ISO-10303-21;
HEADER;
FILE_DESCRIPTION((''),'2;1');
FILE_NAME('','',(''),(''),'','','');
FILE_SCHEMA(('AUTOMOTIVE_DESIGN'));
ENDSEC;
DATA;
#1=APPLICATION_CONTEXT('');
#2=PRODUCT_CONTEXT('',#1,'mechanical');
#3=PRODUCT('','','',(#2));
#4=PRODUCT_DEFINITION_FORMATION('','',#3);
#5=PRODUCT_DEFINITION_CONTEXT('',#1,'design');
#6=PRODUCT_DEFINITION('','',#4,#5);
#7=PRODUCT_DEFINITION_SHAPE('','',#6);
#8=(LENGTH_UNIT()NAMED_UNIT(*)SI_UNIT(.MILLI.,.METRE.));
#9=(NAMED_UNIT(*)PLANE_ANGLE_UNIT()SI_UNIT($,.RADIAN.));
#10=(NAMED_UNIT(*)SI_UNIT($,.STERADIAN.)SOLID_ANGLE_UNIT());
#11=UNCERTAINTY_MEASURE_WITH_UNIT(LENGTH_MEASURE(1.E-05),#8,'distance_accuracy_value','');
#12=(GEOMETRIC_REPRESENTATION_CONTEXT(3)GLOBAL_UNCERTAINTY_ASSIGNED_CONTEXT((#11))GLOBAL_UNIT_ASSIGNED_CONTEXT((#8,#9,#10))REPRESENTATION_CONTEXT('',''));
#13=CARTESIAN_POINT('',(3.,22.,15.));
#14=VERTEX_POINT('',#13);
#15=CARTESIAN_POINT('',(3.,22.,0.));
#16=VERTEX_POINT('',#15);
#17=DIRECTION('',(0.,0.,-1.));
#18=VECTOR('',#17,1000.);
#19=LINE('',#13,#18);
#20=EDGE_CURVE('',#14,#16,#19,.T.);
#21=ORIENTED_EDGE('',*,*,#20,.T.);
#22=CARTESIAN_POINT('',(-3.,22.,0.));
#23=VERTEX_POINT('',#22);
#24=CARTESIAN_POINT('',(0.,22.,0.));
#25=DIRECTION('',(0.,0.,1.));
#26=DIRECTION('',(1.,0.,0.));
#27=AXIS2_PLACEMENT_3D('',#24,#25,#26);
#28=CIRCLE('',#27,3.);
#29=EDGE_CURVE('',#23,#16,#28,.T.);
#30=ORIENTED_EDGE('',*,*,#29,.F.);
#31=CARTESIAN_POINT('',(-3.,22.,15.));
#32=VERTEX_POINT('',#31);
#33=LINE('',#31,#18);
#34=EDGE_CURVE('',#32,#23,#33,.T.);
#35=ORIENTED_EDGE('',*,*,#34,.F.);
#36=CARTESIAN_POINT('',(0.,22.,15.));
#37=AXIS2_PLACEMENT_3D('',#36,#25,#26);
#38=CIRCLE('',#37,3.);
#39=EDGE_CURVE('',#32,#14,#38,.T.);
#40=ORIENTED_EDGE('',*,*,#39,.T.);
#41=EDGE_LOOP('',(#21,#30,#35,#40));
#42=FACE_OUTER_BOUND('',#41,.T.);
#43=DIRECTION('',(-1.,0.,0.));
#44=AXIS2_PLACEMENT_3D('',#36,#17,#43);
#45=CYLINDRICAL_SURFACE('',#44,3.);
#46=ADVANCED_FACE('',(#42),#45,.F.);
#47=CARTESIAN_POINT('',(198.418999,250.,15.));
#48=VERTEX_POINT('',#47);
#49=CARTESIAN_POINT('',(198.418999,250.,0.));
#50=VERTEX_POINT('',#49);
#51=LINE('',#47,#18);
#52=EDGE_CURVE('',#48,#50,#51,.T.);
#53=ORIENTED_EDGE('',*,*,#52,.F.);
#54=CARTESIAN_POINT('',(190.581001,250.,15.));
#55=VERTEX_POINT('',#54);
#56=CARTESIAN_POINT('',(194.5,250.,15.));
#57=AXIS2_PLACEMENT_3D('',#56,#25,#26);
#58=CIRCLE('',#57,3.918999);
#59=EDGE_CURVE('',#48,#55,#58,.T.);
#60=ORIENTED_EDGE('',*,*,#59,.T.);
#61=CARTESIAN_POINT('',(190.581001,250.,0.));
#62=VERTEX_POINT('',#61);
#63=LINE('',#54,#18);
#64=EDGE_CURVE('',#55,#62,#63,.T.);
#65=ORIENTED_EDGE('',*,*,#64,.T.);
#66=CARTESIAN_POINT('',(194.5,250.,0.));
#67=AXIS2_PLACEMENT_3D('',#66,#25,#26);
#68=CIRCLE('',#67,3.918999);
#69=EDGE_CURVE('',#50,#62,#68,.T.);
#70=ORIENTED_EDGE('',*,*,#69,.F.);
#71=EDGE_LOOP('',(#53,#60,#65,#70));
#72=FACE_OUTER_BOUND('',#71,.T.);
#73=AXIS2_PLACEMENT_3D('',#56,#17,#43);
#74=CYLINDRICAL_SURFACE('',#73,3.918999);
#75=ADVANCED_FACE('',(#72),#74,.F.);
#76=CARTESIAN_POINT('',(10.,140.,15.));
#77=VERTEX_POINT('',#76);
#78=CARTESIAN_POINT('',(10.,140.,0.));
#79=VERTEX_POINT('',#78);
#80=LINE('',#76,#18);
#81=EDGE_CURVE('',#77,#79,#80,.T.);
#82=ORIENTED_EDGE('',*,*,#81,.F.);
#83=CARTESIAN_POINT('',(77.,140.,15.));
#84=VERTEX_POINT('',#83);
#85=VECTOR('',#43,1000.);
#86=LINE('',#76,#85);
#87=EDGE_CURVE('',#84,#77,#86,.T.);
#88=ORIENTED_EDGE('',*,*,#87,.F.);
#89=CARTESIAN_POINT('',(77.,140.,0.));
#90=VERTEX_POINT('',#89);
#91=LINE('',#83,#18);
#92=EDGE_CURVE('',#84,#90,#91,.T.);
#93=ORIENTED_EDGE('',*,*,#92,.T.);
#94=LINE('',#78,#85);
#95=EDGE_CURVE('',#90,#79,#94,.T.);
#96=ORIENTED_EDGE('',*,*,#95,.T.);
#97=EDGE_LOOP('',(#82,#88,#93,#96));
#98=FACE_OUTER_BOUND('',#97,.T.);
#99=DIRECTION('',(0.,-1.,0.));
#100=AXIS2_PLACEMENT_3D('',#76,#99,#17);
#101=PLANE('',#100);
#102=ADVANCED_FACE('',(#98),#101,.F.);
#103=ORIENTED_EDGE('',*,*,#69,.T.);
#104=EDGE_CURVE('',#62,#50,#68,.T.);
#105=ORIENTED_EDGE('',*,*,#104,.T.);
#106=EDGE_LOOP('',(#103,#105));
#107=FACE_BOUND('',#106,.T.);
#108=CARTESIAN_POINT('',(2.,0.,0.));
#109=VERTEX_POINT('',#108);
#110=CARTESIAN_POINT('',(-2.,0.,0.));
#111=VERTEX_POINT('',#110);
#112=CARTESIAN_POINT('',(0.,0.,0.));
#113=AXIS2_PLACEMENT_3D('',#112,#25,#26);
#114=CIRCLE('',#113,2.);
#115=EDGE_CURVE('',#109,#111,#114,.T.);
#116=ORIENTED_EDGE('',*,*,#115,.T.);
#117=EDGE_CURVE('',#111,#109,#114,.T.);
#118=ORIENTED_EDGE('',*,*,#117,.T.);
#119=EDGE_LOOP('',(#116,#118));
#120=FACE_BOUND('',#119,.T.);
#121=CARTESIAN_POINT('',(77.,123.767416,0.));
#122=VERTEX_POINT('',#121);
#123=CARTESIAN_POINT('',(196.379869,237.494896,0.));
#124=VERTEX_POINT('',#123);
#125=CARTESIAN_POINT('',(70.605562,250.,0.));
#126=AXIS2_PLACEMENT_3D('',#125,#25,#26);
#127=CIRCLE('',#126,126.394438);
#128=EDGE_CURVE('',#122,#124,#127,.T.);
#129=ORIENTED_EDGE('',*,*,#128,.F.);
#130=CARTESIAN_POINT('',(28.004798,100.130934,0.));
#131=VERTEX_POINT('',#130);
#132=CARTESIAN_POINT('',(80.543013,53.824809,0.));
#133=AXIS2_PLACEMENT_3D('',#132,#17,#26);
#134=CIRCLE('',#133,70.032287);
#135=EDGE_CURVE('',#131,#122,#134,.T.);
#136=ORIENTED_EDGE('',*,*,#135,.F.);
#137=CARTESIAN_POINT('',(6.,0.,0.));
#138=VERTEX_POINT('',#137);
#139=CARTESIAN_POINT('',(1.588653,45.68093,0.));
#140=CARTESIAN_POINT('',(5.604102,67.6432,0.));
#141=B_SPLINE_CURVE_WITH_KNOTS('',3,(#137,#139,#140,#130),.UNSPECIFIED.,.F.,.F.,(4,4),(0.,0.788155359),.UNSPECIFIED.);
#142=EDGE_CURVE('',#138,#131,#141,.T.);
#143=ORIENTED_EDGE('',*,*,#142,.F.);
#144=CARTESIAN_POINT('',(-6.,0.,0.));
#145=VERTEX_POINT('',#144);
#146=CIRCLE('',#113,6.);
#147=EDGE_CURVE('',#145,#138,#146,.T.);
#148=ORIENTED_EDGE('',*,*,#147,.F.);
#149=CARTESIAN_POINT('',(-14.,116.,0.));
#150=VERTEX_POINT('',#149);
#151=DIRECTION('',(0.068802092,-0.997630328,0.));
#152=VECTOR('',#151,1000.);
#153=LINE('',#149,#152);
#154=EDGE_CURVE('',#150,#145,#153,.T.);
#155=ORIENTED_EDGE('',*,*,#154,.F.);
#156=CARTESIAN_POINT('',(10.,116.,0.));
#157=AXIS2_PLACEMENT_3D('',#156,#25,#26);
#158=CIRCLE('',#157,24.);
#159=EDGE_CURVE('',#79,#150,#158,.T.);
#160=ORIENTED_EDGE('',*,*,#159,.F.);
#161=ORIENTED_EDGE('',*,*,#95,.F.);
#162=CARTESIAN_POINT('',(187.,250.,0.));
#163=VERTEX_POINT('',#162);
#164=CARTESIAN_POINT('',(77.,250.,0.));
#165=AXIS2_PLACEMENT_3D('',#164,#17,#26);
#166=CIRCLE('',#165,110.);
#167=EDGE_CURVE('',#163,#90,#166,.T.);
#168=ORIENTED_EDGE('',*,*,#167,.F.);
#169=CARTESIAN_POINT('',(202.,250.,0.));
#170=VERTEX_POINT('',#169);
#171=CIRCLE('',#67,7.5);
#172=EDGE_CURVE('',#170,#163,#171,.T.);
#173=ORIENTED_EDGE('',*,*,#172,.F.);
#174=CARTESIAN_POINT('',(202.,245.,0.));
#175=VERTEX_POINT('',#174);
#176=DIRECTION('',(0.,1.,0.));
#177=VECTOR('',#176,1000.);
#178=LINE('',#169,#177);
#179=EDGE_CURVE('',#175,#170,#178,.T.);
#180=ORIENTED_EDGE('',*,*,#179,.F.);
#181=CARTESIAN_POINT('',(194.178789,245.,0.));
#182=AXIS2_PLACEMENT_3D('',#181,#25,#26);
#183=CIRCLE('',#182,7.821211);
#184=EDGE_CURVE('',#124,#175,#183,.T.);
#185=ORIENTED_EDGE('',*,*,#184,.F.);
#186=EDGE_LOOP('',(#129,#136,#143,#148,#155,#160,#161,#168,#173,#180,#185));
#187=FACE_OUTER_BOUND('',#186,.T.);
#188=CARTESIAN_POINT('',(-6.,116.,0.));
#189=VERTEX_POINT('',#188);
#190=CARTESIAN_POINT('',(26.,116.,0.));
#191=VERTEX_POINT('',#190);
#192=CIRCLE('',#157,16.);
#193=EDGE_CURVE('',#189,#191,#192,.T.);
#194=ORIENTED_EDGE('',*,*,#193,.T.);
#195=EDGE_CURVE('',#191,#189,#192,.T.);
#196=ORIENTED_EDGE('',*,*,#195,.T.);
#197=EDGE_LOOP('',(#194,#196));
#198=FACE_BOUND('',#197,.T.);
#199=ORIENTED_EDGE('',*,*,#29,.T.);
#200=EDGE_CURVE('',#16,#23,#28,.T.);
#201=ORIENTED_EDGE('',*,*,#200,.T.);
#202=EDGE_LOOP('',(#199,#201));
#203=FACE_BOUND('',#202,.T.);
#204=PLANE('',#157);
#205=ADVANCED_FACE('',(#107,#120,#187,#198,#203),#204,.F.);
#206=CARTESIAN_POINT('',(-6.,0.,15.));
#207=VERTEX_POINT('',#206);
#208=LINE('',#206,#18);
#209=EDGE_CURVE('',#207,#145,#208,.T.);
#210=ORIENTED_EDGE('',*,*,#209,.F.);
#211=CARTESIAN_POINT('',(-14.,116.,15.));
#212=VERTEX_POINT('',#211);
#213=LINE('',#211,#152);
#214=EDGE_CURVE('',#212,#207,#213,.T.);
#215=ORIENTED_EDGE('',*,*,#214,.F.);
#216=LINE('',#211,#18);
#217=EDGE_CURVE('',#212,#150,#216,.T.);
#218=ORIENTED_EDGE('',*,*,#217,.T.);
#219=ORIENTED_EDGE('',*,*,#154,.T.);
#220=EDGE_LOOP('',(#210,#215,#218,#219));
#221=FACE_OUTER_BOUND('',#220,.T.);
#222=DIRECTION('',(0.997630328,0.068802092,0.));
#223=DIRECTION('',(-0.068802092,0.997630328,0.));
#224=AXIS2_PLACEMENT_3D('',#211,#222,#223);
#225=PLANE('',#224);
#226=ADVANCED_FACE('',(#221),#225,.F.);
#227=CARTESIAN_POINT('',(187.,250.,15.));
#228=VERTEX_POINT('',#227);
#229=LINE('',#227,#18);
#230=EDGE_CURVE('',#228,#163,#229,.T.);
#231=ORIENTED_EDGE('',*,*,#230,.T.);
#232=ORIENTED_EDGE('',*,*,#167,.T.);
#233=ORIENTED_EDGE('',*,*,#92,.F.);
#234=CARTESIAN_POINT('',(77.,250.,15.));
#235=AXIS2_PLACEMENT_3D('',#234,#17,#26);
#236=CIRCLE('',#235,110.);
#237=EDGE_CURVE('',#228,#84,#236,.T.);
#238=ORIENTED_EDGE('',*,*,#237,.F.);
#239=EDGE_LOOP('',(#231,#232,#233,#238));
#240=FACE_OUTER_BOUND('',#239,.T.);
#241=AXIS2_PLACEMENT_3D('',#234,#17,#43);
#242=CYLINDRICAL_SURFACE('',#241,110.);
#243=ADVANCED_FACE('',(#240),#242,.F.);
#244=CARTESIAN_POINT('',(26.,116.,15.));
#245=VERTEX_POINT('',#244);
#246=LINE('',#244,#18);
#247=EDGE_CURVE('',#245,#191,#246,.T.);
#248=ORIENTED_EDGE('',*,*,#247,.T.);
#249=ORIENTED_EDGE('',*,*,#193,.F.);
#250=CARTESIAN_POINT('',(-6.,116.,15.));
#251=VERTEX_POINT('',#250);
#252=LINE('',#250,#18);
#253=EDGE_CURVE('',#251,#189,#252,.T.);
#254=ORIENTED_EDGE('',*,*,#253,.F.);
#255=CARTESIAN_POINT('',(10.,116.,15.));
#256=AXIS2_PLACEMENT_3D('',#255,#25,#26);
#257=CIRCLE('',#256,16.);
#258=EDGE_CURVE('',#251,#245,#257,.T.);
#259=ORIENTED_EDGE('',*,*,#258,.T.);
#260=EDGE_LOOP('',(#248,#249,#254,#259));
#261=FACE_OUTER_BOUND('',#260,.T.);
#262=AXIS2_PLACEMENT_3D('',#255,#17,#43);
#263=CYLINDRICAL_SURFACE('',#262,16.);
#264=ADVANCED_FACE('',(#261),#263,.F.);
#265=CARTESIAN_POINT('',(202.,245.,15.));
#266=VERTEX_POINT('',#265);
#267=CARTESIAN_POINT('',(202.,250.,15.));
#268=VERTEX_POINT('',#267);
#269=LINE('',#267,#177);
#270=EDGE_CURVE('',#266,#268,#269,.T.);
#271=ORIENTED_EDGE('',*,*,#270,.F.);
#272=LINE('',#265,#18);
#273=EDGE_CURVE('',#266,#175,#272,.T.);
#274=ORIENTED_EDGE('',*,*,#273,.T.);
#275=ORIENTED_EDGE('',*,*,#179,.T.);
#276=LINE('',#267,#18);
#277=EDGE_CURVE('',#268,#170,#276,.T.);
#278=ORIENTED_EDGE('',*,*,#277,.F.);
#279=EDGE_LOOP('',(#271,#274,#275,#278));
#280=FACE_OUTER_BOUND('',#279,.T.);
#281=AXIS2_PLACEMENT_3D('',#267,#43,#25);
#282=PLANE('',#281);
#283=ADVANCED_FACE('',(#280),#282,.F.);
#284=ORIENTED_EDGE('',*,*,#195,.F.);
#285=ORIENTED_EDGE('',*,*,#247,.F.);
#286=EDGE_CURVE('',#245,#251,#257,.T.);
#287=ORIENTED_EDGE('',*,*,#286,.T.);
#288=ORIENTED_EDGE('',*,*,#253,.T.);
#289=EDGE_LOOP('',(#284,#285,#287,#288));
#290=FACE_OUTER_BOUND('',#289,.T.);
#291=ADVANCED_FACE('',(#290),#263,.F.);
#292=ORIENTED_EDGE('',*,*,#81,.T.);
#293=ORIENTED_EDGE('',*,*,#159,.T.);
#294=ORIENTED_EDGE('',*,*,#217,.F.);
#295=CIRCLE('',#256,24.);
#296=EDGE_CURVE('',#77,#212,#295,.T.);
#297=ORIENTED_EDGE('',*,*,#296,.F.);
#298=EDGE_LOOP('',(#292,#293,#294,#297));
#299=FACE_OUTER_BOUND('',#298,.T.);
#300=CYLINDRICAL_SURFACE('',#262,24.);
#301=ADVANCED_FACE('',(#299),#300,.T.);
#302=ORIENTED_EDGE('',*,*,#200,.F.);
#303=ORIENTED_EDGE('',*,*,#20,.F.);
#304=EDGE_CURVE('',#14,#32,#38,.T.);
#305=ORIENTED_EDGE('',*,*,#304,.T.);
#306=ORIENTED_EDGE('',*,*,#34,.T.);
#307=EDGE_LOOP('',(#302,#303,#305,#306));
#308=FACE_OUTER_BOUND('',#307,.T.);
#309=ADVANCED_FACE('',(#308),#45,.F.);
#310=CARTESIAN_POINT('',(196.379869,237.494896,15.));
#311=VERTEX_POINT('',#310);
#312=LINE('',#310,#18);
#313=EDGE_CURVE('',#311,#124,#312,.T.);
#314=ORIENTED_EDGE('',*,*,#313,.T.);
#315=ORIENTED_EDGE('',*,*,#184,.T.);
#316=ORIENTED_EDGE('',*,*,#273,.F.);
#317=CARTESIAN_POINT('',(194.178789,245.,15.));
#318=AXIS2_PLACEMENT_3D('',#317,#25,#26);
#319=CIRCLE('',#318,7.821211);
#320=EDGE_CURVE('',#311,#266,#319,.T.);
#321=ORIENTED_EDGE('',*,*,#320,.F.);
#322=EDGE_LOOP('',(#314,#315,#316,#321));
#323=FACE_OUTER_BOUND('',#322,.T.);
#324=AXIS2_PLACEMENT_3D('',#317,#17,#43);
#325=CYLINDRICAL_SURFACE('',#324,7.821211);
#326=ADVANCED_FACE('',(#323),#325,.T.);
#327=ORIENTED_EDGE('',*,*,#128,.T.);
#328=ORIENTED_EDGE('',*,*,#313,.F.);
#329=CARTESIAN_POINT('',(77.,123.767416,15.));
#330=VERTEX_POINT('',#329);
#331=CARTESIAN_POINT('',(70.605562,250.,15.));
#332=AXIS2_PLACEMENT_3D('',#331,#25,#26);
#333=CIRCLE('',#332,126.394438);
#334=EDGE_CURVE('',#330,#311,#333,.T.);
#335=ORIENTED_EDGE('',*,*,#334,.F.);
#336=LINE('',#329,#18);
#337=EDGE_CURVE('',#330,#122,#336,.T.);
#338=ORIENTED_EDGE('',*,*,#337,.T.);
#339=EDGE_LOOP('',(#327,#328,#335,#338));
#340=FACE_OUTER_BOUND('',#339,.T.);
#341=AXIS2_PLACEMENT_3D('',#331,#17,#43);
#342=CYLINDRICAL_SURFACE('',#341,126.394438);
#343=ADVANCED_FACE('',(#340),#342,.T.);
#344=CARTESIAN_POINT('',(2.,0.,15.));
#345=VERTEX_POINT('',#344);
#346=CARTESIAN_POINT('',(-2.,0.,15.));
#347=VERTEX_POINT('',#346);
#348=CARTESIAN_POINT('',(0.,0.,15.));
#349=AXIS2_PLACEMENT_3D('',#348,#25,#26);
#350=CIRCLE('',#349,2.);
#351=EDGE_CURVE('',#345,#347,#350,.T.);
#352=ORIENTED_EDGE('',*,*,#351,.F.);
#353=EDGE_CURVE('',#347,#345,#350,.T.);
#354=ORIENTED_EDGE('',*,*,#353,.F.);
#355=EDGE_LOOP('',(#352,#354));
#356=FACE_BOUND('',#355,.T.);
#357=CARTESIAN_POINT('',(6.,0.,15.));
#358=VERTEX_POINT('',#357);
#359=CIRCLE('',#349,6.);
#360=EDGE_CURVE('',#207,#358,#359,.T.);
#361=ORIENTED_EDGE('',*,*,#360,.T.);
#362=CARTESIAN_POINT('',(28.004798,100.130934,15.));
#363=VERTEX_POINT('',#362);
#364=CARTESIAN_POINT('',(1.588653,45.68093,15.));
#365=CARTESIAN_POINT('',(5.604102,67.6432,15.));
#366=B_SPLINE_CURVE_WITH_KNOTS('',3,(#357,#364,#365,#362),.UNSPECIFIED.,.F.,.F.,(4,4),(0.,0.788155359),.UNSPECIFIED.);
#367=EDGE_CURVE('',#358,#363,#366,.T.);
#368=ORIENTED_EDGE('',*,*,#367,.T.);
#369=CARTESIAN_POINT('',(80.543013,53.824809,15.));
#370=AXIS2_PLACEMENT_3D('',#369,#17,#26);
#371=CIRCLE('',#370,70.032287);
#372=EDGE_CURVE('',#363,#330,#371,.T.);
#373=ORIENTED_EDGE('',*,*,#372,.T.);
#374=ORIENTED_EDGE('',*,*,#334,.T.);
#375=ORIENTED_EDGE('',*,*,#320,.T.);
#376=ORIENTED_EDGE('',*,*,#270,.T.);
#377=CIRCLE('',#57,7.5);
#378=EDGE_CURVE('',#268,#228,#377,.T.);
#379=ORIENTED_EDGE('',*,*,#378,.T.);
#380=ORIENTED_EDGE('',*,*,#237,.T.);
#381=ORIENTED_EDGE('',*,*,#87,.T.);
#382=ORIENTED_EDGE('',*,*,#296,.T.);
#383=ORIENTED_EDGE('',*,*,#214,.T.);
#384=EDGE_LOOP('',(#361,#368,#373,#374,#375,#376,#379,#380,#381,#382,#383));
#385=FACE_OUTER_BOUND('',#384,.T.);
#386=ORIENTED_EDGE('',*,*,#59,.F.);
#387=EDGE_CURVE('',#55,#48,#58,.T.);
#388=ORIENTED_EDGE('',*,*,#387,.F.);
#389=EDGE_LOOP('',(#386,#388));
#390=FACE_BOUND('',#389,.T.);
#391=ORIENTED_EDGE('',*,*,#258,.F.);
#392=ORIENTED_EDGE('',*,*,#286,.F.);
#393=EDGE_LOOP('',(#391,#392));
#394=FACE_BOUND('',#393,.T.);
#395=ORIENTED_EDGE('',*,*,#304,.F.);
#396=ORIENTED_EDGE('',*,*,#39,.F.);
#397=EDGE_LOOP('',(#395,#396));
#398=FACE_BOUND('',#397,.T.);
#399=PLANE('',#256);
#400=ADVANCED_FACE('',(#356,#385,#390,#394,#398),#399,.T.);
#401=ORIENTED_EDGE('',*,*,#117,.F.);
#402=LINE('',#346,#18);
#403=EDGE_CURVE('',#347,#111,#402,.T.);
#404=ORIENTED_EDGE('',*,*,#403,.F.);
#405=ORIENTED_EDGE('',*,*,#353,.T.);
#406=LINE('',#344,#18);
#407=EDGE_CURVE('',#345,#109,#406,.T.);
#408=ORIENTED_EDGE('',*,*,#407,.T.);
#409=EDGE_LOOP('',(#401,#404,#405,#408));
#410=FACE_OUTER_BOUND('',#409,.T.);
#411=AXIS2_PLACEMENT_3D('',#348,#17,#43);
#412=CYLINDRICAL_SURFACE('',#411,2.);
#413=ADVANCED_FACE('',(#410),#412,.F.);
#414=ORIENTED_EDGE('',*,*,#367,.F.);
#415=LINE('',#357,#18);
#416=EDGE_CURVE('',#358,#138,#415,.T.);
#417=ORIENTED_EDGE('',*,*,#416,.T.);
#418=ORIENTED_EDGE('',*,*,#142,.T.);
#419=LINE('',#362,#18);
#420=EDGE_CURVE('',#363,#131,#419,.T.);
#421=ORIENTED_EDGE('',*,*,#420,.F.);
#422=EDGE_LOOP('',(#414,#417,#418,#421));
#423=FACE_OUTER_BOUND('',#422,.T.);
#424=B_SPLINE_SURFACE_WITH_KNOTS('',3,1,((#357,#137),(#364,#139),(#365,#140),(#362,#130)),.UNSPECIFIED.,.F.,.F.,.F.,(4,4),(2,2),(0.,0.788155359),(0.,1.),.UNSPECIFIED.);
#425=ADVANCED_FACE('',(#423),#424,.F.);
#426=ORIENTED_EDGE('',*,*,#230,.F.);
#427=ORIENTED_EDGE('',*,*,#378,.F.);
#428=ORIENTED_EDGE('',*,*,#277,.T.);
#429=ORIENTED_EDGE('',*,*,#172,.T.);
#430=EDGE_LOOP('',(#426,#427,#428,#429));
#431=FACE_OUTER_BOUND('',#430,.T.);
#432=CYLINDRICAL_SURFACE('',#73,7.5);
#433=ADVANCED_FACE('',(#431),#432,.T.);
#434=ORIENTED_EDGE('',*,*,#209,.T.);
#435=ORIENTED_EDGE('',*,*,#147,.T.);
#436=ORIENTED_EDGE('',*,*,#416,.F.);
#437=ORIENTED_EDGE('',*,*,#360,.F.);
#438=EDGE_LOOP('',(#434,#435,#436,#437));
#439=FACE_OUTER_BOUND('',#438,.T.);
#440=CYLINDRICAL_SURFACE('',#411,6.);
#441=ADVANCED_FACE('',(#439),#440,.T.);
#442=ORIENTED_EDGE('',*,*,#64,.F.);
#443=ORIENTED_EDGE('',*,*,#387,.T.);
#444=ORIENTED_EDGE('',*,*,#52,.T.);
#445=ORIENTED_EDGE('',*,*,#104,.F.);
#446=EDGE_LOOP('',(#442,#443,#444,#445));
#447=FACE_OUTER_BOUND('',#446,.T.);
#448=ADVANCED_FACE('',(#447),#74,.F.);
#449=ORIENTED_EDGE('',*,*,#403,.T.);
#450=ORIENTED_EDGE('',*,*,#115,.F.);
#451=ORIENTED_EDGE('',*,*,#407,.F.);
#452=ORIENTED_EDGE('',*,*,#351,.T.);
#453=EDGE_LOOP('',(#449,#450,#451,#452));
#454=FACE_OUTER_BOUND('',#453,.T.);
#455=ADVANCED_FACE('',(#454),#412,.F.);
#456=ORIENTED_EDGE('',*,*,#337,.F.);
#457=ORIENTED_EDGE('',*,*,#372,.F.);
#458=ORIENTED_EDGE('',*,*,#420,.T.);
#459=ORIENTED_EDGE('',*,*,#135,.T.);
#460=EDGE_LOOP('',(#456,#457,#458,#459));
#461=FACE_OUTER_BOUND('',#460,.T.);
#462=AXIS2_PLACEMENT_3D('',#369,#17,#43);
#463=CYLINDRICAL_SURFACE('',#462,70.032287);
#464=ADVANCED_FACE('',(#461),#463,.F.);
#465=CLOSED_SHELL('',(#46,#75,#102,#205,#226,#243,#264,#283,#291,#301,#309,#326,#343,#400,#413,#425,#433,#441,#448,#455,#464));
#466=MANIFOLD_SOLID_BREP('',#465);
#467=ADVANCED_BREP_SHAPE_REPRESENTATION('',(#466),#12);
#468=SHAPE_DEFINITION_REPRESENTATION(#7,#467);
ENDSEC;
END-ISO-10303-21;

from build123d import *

# Parameters (mm, degrees)
SKETCH_1_R      = 2
SKETCH_1_R_2    = 16
SKETCH_1_R_3    = 3.91899873
SKETCH_1_R_4    = 3
EXTRUDE_3_DEPTH = 15


with BuildPart() as part:
    # 草图1 → 凸台-拉伸3 (new body)
    with BuildSketch(Plane.XY):
        with BuildLine():
            Line((-14, 116), (-6, 0))
            ThreePointArc((-6, 0), (0, -6), (6, 0))
            add(Edge.make_bspline(
                [(6, 0), (1.588652615, 45.680929706), (5.604102499, 67.643200211), (28.004797731, 100.13093391)],
                knots=[0, 0, 0, 0, 0.788155359, 0.788155359, 0.788155359, 0.788155359], degree=3))
            ThreePointArc((28.004797731, 100.13093391), (50.113637924, 116.900750568), (77, 123.767416406))
            ThreePointArc((77, 123.767416406), (157.787149523, 158.485384951), (196.379869136, 237.494896157))
            ThreePointArc((196.379869136, 237.494896157), (200.439238403, 240.311917913), (202, 245))
            Line((202, 245), (202, 250))
            ThreePointArc((202, 250), (194.5, 257.5), (187, 250))
            ThreePointArc((187, 250), (154.781745931, 172.218254069), (77, 140))
            Line((77, 140), (10, 140))
            ThreePointArc((10, 140), (-6.970562748, 132.970562748), (-14, 116))
        make_face()
        Circle(SKETCH_1_R, mode=Mode.SUBTRACT)
        with Locations((10, 116)):
            Circle(SKETCH_1_R_2, mode=Mode.SUBTRACT)
        with Locations((194.5, 250)):
            Circle(SKETCH_1_R_3, mode=Mode.SUBTRACT)
        with Locations((0, 22)):
            Circle(SKETCH_1_R_4, mode=Mode.SUBTRACT)
    extrude(amount=EXTRUDE_3_DEPTH)


solid = part.part
